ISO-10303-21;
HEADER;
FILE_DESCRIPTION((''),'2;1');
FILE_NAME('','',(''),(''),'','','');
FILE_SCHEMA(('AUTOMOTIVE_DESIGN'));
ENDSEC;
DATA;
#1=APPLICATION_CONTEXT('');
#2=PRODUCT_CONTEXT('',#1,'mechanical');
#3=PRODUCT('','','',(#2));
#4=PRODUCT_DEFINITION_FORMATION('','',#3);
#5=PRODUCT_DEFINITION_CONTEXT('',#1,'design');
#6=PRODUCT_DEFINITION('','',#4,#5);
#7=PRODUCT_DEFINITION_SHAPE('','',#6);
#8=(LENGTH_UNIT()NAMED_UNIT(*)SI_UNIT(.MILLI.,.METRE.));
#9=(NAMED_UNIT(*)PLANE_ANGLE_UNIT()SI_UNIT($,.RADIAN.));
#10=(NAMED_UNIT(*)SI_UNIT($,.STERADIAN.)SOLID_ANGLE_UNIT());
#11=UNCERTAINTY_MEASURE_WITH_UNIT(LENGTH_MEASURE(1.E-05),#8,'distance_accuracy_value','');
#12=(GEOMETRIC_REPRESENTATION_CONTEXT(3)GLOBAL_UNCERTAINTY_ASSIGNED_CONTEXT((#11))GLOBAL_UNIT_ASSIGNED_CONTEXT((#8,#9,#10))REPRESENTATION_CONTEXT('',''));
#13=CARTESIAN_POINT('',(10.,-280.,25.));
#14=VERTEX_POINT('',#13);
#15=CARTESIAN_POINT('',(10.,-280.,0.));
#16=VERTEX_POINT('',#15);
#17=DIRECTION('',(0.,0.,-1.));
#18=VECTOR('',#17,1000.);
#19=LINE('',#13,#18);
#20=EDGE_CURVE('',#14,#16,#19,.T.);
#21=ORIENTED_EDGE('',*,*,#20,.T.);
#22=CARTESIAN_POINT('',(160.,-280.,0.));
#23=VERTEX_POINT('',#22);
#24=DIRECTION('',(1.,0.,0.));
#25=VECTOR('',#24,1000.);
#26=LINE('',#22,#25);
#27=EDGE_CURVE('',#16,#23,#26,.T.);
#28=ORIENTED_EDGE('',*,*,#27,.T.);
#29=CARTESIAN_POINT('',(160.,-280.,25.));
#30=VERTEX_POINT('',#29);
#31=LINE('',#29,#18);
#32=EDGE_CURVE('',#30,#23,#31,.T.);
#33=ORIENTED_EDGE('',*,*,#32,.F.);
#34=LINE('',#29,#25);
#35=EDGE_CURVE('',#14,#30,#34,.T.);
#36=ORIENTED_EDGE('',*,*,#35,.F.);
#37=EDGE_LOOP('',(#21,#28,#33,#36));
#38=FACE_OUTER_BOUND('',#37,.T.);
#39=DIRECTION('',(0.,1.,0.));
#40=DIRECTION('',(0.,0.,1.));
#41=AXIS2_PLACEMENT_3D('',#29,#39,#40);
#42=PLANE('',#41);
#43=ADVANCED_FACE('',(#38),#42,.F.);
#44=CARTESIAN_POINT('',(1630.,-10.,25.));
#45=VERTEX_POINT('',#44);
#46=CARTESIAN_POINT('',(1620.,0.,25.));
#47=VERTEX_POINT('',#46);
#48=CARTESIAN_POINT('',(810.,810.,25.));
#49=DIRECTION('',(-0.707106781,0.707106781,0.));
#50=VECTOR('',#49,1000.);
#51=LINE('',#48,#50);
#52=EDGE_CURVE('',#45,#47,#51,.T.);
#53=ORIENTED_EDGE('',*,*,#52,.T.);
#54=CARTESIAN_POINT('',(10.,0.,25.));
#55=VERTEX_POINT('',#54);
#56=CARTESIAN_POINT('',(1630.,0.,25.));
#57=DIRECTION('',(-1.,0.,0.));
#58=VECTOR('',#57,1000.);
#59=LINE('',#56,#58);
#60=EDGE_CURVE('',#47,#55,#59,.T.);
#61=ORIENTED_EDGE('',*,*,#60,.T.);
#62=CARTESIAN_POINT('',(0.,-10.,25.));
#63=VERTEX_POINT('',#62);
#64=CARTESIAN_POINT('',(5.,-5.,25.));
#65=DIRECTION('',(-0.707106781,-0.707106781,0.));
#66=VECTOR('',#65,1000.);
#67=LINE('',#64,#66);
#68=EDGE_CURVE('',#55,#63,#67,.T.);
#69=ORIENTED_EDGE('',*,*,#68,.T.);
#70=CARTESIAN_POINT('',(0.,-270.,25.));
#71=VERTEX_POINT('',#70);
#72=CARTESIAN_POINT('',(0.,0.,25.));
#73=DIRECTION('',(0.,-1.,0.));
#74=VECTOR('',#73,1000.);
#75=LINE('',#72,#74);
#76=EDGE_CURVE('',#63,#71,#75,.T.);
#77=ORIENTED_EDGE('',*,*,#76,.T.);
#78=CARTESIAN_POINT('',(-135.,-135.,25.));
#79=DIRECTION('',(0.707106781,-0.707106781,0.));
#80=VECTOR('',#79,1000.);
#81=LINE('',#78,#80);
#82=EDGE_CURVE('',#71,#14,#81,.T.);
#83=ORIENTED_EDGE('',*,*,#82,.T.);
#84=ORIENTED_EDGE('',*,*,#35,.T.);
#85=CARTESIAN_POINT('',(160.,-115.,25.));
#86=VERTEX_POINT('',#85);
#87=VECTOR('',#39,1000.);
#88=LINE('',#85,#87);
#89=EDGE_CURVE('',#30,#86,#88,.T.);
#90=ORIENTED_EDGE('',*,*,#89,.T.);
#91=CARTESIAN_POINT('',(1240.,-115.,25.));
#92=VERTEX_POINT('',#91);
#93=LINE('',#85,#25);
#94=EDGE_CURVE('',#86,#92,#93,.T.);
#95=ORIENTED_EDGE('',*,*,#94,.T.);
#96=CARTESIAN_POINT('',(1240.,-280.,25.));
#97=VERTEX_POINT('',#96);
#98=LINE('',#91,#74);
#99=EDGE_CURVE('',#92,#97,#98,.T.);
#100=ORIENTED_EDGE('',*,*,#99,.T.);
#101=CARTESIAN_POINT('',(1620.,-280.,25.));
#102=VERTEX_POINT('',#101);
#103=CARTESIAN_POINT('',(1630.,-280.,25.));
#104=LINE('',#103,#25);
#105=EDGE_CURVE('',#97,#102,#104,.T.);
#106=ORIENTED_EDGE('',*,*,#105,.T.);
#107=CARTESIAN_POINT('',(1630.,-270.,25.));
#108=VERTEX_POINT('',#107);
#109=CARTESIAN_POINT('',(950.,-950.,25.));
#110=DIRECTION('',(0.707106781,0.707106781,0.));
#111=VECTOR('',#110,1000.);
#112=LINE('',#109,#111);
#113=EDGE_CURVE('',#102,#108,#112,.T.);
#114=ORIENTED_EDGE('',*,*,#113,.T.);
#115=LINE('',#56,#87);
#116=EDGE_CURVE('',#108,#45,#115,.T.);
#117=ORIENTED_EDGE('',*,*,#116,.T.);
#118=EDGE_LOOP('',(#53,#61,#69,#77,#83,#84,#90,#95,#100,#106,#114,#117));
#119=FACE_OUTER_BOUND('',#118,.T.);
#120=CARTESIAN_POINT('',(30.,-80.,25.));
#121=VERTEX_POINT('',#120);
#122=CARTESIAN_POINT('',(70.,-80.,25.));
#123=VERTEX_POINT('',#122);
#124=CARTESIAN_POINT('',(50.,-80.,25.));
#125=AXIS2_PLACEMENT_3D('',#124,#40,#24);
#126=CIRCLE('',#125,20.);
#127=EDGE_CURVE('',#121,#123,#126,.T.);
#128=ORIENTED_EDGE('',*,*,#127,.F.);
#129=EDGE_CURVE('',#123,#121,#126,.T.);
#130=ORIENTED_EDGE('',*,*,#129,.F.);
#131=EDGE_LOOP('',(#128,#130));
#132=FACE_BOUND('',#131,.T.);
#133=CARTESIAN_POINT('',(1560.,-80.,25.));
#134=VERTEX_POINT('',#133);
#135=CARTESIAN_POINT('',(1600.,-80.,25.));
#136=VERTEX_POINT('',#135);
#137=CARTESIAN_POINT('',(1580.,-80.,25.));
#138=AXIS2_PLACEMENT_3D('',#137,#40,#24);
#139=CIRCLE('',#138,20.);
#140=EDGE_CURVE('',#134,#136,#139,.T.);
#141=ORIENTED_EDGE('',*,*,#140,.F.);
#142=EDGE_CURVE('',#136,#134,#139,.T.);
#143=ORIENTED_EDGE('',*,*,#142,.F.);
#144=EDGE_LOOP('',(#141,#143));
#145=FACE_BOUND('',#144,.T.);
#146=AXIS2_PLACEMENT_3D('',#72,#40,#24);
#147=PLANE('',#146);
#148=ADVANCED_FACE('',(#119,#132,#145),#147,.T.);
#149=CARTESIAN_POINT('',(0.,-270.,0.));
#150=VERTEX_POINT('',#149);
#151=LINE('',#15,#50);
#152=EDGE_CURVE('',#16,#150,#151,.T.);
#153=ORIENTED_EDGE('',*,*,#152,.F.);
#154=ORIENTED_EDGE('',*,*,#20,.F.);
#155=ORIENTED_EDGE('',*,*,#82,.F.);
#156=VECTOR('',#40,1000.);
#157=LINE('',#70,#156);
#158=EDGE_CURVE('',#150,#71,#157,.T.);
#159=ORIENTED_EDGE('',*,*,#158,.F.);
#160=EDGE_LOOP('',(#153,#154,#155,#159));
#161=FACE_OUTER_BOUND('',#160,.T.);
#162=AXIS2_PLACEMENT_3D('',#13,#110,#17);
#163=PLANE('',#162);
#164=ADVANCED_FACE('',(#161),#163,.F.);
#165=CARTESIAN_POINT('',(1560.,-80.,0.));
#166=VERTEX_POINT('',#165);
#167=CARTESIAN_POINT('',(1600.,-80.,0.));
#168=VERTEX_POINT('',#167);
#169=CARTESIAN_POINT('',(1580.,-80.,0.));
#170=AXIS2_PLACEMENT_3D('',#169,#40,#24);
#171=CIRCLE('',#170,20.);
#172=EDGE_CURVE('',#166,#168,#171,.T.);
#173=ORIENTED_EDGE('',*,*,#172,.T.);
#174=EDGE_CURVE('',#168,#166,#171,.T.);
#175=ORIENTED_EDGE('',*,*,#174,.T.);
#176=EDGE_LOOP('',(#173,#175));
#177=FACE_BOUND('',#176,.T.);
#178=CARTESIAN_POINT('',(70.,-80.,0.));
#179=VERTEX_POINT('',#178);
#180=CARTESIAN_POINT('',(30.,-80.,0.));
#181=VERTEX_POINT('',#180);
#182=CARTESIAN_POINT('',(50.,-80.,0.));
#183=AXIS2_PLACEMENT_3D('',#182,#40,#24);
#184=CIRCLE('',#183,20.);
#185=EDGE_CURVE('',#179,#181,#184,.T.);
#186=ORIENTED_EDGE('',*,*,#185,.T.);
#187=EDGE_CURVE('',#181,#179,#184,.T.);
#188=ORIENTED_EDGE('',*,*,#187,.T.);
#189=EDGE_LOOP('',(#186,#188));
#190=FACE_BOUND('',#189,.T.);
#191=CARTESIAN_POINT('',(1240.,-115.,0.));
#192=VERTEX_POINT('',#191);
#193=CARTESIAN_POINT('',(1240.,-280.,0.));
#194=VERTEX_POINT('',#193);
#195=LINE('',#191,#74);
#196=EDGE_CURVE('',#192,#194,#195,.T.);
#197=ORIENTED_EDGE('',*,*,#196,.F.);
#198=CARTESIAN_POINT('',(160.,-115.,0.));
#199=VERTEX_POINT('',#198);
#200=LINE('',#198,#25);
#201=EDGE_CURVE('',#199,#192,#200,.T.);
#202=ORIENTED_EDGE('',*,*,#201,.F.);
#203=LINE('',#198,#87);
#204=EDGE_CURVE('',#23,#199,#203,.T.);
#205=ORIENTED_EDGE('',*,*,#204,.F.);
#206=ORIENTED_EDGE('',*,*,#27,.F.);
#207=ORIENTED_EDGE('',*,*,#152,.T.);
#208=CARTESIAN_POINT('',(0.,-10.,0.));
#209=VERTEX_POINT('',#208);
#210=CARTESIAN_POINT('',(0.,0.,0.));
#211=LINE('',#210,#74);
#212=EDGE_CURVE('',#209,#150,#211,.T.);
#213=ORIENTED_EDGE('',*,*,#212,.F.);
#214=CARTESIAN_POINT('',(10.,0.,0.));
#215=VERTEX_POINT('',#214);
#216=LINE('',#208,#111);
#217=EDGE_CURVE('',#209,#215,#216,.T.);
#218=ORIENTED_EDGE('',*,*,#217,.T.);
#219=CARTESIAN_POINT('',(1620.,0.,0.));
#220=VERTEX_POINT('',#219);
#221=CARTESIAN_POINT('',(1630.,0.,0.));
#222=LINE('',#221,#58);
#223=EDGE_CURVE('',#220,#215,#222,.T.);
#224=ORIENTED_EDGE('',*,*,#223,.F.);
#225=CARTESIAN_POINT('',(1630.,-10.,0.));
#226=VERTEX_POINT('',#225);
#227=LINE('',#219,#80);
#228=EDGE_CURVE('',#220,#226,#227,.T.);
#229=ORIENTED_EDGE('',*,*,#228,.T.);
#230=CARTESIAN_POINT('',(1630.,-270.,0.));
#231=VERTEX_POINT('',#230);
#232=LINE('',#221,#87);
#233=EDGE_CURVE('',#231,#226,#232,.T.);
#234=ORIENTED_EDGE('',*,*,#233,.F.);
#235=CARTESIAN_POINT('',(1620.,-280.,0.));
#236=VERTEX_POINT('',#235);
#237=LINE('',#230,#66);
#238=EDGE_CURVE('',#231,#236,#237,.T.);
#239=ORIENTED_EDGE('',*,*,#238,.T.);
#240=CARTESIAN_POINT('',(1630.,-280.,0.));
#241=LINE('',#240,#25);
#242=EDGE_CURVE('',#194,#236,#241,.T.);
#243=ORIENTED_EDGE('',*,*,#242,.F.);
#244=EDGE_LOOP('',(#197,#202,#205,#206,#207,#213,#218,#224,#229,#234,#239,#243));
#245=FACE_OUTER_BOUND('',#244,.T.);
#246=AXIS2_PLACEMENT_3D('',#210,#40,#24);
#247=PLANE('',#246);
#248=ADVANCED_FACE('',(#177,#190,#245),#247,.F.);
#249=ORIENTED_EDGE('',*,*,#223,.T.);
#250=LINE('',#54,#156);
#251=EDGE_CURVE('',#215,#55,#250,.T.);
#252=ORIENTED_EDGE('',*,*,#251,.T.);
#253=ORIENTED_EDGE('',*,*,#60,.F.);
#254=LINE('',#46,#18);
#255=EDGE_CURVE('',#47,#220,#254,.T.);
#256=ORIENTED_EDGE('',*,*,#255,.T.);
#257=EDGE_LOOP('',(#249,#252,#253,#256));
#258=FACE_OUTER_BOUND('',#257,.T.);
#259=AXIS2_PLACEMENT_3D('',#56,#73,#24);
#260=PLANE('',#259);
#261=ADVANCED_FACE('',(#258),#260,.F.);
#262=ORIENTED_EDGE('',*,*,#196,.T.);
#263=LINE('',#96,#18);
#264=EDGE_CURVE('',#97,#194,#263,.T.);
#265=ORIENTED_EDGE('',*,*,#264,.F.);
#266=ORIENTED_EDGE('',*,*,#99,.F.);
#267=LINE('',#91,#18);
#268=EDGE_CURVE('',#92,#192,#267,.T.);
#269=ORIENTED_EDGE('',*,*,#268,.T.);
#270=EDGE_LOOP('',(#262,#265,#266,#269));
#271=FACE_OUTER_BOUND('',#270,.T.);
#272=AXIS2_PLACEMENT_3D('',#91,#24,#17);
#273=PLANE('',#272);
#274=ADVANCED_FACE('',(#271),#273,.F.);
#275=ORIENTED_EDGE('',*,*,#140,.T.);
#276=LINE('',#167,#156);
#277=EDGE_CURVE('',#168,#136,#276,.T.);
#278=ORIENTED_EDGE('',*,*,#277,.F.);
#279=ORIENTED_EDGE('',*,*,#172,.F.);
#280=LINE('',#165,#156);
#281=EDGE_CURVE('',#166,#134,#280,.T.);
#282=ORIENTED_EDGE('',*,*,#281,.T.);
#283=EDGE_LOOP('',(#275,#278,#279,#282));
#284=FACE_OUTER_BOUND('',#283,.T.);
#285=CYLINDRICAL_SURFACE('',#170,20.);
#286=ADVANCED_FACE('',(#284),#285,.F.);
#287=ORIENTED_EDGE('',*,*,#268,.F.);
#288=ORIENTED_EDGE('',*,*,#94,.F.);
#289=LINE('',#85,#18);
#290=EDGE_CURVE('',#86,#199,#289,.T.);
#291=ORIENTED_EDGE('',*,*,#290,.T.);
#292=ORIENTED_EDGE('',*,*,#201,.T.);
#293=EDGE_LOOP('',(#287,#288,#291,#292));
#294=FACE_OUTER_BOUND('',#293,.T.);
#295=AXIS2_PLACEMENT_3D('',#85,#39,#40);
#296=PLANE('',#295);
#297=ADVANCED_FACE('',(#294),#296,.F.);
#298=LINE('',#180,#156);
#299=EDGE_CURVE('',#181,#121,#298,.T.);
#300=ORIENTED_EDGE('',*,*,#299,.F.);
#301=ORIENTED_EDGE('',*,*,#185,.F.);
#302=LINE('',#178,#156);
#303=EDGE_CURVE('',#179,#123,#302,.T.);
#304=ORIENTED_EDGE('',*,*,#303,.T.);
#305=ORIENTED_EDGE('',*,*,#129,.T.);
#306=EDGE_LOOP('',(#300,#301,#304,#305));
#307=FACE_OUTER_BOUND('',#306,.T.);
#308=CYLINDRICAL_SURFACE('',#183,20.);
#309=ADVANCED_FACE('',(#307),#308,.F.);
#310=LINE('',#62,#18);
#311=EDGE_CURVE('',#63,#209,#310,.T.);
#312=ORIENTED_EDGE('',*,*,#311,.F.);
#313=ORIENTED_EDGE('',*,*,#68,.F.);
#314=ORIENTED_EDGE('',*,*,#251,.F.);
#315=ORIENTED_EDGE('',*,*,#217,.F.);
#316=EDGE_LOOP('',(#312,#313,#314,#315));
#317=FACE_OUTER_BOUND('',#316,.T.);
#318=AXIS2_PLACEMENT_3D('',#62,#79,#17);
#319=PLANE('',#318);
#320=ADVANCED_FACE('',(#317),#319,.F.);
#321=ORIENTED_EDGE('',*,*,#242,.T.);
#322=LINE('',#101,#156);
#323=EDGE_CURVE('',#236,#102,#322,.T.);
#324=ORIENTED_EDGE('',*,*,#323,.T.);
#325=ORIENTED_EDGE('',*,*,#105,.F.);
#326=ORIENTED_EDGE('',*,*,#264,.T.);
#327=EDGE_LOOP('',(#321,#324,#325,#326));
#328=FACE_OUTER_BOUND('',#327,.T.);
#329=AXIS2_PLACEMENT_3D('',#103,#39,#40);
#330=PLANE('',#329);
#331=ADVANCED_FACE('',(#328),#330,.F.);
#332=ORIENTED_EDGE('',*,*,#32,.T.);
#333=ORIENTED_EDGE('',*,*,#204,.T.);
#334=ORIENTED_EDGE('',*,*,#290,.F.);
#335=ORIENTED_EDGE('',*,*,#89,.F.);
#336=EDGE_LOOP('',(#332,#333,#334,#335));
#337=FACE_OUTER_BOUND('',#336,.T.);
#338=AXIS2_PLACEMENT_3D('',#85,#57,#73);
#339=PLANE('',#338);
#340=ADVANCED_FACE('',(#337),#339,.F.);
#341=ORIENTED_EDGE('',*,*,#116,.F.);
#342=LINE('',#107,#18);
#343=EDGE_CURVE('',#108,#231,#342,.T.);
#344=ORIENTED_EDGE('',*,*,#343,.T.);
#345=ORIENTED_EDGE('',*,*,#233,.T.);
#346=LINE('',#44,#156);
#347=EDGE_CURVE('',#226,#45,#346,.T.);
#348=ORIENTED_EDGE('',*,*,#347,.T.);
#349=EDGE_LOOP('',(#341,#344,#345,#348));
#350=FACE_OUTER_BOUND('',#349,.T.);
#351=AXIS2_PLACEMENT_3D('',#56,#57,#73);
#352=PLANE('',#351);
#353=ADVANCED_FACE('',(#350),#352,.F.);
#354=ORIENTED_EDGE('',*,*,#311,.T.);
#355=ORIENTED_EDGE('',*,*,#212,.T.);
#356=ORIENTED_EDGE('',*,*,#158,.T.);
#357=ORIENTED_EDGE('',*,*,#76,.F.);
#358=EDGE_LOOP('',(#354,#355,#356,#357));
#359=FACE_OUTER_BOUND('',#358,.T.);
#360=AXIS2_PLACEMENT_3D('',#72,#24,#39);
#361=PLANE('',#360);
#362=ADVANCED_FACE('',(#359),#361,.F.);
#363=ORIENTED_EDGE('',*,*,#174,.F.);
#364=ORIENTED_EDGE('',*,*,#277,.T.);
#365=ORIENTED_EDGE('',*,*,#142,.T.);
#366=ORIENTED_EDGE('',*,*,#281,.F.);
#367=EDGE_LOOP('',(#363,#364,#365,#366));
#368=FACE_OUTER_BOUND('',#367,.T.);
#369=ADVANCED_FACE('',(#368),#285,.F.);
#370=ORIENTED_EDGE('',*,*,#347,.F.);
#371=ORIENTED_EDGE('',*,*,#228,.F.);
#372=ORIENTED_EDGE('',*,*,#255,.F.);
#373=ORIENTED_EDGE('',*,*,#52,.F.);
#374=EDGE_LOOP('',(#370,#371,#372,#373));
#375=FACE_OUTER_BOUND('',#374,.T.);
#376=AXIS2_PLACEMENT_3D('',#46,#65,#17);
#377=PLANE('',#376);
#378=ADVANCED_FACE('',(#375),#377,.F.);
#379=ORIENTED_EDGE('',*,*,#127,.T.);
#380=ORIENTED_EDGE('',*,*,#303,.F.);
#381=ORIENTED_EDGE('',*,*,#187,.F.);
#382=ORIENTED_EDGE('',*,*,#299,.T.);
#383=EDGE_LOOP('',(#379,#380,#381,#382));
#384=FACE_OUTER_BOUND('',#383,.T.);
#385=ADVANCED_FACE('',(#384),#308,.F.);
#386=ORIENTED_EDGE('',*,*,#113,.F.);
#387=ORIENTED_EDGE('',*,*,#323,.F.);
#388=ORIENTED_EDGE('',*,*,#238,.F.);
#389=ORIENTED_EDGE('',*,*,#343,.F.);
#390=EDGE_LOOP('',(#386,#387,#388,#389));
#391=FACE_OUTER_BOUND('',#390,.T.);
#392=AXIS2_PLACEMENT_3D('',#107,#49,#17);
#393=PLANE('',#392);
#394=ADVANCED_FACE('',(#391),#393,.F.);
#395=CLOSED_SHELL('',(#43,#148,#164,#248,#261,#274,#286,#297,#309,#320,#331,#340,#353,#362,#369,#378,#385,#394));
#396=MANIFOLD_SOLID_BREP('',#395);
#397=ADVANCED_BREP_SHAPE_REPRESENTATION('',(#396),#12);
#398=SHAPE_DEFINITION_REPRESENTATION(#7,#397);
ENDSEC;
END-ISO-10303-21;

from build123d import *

# Parameters (mm, degrees)
EXTRUDE_1_DEPTH          = 25
CHAMFER_1_SIZE           = 10
CUT_EXTRUDE_1_DEPTH      = 1655.063178963
CUT_EXTRUDE_1_DEPTH_BACK = 1655.063178963
SKETCH_2_R               = 20


with BuildPart() as part:
    # 草图1 → 凸台-拉伸1 (new body)
    with BuildSketch(Plane.XY):
        Polygon((160, -280), (0, -280), (0, 0), (1630, 0), (1630, -280), (1240, -280), (1240, -115), (160, -115), align=None)
    extrude(amount=EXTRUDE_1_DEPTH)

    # 倒角1
    chamfer_1_edges = [part.edges().sort_by_distance(p)[0] for p in [
        (0, -280, 12.5),
        (0, 0, 12.5),
        (1630, 0, 12.5),
        (1630, -280, 12.5),
    ]]
    chamfer(chamfer_1_edges, length=CHAMFER_1_SIZE)

    # 草图2 → 切除-拉伸1 (cut, two sides: drawn at the far end of the back side and taken through both)
    with BuildSketch(Plane.XY.offset(25).offset(-CUT_EXTRUDE_1_DEPTH_BACK)):
        with Locations((50, -80)):
            Circle(SKETCH_2_R)
        with Locations((1580, -80)):
            Circle(SKETCH_2_R)
    extrude(amount=CUT_EXTRUDE_1_DEPTH + CUT_EXTRUDE_1_DEPTH_BACK, mode=Mode.SUBTRACT)


solid = part.part
